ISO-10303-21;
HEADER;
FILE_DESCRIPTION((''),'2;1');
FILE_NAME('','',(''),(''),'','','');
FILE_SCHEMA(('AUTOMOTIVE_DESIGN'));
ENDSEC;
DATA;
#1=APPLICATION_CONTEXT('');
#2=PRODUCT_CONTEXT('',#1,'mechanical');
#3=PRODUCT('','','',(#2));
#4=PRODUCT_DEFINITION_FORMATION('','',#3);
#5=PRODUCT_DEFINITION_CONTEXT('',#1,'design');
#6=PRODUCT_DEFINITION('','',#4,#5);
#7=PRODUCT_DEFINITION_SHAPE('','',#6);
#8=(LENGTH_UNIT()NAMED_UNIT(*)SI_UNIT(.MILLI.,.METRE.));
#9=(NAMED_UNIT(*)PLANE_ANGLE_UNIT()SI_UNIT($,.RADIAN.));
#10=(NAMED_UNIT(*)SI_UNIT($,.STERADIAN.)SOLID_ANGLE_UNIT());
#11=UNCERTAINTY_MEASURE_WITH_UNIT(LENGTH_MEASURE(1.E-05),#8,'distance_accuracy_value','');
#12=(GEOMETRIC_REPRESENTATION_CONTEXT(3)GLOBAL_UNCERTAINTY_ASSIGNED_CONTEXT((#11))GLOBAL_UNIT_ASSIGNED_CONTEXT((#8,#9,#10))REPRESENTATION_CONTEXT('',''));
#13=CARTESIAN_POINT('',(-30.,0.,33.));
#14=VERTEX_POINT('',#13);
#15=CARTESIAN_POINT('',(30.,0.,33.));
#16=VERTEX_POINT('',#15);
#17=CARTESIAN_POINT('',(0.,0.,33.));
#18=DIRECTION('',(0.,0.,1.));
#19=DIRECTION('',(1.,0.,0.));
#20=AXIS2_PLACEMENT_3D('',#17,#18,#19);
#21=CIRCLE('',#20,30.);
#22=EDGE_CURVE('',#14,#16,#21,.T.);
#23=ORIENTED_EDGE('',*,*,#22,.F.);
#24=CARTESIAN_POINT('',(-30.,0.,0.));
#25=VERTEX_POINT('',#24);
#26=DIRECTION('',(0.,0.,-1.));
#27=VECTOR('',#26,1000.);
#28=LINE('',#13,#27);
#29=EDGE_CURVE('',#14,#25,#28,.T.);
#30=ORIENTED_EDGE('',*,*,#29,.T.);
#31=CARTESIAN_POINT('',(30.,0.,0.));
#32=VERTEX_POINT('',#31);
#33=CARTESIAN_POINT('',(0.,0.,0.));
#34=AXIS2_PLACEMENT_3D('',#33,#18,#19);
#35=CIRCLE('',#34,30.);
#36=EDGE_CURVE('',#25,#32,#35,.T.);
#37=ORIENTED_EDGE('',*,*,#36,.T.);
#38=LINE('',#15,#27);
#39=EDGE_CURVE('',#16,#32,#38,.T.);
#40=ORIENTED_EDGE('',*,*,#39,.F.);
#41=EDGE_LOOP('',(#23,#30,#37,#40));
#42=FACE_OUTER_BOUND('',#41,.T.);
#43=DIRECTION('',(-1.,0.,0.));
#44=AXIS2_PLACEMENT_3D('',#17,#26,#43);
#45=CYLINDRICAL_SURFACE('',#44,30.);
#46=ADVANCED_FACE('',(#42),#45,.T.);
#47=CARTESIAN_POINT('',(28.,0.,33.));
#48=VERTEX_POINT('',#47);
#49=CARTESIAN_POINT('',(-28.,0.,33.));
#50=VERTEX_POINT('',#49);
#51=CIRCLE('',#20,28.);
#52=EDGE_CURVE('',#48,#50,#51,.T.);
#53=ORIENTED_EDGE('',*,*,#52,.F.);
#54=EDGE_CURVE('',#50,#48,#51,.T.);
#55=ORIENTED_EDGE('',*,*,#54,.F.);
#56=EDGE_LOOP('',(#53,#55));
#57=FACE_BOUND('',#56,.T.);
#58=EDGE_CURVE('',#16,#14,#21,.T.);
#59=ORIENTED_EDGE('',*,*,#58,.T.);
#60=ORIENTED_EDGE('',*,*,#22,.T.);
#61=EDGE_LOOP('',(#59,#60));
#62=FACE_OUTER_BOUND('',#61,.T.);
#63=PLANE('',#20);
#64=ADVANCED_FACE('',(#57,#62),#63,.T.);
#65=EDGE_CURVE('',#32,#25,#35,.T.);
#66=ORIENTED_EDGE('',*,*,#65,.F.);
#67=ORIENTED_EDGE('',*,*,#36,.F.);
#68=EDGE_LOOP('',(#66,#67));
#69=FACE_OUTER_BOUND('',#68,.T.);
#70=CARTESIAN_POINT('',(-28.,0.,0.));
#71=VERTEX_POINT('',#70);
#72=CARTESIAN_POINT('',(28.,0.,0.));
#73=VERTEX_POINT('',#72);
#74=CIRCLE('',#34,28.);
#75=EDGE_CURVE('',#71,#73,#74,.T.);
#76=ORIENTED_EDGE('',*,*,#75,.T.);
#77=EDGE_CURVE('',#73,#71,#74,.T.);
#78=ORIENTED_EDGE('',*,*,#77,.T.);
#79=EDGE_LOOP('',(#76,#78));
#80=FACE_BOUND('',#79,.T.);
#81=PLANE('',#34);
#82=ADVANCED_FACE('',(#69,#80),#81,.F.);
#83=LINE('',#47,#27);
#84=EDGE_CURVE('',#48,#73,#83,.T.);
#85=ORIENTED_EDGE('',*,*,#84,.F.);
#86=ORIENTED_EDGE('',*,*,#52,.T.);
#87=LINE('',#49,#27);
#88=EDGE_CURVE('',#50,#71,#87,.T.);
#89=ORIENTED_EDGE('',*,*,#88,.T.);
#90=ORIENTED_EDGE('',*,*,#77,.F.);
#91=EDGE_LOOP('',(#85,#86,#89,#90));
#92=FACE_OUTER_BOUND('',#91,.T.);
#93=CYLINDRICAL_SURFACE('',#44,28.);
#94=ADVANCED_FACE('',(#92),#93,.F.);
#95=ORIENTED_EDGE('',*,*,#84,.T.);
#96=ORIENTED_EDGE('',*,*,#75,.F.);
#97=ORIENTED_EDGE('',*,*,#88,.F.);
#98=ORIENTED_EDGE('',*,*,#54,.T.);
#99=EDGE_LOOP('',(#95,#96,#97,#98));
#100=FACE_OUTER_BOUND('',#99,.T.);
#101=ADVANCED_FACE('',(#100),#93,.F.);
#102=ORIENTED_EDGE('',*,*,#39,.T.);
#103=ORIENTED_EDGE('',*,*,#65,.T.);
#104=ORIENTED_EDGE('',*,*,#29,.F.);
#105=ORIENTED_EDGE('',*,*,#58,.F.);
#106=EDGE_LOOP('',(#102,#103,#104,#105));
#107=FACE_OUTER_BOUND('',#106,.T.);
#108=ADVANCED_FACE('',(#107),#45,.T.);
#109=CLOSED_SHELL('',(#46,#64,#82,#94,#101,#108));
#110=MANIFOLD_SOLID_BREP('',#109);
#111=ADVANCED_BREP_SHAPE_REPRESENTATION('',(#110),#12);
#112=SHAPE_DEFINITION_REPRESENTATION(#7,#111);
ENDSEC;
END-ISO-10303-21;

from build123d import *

# Parameters (mm, degrees)
SKETCH1_R           = 30
SKETCH1_R_2         = 28
BOSS_EXTRUDE1_DEPTH = 33


with BuildPart() as part:
    # Sketch1 → Boss-Extrude1 (new body)
    with BuildSketch(Plane.XY):
        Circle(SKETCH1_R)
        Circle(SKETCH1_R_2, mode=Mode.SUBTRACT)
    extrude(amount=BOSS_EXTRUDE1_DEPTH)


solid = part.part
